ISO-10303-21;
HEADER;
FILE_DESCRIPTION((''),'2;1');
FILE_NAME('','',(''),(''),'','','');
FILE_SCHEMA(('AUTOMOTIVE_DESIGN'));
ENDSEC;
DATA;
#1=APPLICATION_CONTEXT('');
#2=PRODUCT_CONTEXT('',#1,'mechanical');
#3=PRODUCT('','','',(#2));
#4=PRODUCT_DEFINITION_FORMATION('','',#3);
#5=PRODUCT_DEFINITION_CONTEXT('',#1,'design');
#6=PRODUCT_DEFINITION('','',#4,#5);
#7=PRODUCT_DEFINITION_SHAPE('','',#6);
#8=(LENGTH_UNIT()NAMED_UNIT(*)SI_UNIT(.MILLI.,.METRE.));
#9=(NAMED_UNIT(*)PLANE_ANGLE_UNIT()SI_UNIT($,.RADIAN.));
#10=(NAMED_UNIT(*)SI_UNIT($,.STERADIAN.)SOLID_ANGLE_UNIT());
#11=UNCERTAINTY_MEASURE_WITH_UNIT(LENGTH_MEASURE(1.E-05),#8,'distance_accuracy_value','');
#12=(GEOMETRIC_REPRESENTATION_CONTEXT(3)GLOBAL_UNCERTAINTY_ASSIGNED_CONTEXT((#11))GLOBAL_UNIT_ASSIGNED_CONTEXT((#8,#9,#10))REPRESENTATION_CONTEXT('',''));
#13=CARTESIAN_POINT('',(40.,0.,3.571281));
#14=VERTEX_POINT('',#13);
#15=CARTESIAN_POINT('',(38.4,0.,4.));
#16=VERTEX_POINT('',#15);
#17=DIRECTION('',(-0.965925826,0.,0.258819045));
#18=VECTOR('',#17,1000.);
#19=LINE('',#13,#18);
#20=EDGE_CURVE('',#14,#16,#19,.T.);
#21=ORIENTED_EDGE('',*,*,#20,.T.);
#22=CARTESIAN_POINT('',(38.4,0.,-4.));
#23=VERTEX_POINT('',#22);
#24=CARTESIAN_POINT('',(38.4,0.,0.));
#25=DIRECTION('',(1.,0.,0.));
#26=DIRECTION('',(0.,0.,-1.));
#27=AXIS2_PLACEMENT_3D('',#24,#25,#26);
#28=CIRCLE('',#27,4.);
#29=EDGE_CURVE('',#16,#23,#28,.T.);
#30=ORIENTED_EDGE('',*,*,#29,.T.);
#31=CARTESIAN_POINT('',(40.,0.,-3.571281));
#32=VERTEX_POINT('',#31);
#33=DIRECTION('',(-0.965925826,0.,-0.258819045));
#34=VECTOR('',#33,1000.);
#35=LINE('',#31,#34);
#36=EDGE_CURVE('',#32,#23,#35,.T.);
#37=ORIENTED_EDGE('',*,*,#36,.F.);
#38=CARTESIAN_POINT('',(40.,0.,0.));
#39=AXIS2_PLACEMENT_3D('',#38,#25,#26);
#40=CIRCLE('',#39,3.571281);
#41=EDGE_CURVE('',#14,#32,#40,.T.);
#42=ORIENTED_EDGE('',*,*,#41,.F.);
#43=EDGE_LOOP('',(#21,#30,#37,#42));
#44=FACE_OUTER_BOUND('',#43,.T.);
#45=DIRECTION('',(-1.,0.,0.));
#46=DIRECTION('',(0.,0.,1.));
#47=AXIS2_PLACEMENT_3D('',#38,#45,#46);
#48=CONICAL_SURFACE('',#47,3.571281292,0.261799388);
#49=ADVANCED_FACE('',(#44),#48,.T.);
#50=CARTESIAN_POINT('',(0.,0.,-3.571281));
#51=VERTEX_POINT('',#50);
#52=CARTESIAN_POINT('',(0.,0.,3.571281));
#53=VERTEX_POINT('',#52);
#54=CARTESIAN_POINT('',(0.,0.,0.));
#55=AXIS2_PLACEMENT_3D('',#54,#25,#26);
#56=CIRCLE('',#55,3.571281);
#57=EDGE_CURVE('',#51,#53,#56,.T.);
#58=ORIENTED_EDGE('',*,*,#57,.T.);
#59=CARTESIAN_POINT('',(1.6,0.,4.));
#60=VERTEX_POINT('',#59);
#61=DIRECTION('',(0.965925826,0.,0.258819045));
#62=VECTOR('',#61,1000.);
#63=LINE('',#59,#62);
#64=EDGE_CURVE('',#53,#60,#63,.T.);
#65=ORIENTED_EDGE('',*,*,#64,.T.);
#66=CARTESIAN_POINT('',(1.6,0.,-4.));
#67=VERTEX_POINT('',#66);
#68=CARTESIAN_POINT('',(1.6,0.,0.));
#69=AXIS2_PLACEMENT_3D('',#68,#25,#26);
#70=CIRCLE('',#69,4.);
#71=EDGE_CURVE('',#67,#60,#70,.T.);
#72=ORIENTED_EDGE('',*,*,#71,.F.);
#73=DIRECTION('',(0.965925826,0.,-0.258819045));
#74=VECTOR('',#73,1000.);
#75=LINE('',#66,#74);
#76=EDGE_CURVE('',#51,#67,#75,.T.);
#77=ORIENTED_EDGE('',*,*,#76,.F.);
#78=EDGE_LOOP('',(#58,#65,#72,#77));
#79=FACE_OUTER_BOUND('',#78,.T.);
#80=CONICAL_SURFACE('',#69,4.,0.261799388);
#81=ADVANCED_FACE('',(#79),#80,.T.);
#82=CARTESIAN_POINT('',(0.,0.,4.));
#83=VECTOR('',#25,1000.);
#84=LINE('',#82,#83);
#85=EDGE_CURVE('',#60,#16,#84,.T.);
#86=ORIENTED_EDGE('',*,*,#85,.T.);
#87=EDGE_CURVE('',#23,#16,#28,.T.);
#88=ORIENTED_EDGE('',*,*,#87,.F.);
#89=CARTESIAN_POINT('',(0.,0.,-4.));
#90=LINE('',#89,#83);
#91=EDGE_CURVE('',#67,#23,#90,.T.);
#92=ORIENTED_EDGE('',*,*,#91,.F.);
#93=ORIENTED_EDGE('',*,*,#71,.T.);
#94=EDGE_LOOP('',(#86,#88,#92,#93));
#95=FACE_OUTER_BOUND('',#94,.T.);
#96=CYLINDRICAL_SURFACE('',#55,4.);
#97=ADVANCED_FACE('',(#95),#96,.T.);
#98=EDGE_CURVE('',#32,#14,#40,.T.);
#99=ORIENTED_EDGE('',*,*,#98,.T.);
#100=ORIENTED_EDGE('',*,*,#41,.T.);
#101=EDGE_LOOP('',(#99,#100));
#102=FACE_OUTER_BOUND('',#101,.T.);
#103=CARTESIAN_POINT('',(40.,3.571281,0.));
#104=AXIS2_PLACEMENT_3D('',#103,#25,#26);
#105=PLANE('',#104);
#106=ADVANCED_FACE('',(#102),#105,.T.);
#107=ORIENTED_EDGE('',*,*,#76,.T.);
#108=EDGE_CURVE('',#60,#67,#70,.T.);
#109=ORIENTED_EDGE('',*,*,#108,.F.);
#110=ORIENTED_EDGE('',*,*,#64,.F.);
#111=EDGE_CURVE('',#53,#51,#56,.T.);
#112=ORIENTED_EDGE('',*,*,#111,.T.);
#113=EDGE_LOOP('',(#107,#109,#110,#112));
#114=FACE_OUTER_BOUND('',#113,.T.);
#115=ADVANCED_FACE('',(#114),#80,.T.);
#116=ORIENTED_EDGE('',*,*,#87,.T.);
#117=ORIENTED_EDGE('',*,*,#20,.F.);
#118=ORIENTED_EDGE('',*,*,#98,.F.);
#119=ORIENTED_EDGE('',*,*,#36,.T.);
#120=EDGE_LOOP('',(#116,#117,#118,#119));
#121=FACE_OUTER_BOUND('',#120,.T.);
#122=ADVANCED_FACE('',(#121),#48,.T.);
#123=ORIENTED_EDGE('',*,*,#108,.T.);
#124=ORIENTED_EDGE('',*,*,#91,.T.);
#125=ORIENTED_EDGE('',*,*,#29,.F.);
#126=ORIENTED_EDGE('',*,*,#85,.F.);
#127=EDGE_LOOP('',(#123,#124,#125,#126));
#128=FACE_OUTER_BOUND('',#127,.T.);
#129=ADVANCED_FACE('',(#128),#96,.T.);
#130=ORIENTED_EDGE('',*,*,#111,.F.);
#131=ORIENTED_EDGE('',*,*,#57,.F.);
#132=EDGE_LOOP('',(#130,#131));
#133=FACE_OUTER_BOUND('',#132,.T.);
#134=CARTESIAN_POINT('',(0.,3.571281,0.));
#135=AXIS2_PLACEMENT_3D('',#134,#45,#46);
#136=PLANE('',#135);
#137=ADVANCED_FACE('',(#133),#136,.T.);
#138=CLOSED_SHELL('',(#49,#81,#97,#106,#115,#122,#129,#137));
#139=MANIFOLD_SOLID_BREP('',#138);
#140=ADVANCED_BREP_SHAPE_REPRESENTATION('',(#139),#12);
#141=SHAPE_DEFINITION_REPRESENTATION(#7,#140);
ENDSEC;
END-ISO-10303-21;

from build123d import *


with BuildPart() as part:
    # Dimensioned Sketch → Base-Revolve (revolve)
    with BuildSketch(Plane.XY, mode=Mode.PRIVATE) as base_revolve_sk:
        Polygon((0, 0), (40, 0), (40, 3.571281292), (38.4, 4), (1.6, 4), (0, 3.571281292), align=None)
    revolve(base_revolve_sk.sketch.rotate(Axis((0, 0, 0), (-1, 0, 0)), 90), axis=Axis((0, 0, 0), (-1, 0, 0)))


solid = part.part
